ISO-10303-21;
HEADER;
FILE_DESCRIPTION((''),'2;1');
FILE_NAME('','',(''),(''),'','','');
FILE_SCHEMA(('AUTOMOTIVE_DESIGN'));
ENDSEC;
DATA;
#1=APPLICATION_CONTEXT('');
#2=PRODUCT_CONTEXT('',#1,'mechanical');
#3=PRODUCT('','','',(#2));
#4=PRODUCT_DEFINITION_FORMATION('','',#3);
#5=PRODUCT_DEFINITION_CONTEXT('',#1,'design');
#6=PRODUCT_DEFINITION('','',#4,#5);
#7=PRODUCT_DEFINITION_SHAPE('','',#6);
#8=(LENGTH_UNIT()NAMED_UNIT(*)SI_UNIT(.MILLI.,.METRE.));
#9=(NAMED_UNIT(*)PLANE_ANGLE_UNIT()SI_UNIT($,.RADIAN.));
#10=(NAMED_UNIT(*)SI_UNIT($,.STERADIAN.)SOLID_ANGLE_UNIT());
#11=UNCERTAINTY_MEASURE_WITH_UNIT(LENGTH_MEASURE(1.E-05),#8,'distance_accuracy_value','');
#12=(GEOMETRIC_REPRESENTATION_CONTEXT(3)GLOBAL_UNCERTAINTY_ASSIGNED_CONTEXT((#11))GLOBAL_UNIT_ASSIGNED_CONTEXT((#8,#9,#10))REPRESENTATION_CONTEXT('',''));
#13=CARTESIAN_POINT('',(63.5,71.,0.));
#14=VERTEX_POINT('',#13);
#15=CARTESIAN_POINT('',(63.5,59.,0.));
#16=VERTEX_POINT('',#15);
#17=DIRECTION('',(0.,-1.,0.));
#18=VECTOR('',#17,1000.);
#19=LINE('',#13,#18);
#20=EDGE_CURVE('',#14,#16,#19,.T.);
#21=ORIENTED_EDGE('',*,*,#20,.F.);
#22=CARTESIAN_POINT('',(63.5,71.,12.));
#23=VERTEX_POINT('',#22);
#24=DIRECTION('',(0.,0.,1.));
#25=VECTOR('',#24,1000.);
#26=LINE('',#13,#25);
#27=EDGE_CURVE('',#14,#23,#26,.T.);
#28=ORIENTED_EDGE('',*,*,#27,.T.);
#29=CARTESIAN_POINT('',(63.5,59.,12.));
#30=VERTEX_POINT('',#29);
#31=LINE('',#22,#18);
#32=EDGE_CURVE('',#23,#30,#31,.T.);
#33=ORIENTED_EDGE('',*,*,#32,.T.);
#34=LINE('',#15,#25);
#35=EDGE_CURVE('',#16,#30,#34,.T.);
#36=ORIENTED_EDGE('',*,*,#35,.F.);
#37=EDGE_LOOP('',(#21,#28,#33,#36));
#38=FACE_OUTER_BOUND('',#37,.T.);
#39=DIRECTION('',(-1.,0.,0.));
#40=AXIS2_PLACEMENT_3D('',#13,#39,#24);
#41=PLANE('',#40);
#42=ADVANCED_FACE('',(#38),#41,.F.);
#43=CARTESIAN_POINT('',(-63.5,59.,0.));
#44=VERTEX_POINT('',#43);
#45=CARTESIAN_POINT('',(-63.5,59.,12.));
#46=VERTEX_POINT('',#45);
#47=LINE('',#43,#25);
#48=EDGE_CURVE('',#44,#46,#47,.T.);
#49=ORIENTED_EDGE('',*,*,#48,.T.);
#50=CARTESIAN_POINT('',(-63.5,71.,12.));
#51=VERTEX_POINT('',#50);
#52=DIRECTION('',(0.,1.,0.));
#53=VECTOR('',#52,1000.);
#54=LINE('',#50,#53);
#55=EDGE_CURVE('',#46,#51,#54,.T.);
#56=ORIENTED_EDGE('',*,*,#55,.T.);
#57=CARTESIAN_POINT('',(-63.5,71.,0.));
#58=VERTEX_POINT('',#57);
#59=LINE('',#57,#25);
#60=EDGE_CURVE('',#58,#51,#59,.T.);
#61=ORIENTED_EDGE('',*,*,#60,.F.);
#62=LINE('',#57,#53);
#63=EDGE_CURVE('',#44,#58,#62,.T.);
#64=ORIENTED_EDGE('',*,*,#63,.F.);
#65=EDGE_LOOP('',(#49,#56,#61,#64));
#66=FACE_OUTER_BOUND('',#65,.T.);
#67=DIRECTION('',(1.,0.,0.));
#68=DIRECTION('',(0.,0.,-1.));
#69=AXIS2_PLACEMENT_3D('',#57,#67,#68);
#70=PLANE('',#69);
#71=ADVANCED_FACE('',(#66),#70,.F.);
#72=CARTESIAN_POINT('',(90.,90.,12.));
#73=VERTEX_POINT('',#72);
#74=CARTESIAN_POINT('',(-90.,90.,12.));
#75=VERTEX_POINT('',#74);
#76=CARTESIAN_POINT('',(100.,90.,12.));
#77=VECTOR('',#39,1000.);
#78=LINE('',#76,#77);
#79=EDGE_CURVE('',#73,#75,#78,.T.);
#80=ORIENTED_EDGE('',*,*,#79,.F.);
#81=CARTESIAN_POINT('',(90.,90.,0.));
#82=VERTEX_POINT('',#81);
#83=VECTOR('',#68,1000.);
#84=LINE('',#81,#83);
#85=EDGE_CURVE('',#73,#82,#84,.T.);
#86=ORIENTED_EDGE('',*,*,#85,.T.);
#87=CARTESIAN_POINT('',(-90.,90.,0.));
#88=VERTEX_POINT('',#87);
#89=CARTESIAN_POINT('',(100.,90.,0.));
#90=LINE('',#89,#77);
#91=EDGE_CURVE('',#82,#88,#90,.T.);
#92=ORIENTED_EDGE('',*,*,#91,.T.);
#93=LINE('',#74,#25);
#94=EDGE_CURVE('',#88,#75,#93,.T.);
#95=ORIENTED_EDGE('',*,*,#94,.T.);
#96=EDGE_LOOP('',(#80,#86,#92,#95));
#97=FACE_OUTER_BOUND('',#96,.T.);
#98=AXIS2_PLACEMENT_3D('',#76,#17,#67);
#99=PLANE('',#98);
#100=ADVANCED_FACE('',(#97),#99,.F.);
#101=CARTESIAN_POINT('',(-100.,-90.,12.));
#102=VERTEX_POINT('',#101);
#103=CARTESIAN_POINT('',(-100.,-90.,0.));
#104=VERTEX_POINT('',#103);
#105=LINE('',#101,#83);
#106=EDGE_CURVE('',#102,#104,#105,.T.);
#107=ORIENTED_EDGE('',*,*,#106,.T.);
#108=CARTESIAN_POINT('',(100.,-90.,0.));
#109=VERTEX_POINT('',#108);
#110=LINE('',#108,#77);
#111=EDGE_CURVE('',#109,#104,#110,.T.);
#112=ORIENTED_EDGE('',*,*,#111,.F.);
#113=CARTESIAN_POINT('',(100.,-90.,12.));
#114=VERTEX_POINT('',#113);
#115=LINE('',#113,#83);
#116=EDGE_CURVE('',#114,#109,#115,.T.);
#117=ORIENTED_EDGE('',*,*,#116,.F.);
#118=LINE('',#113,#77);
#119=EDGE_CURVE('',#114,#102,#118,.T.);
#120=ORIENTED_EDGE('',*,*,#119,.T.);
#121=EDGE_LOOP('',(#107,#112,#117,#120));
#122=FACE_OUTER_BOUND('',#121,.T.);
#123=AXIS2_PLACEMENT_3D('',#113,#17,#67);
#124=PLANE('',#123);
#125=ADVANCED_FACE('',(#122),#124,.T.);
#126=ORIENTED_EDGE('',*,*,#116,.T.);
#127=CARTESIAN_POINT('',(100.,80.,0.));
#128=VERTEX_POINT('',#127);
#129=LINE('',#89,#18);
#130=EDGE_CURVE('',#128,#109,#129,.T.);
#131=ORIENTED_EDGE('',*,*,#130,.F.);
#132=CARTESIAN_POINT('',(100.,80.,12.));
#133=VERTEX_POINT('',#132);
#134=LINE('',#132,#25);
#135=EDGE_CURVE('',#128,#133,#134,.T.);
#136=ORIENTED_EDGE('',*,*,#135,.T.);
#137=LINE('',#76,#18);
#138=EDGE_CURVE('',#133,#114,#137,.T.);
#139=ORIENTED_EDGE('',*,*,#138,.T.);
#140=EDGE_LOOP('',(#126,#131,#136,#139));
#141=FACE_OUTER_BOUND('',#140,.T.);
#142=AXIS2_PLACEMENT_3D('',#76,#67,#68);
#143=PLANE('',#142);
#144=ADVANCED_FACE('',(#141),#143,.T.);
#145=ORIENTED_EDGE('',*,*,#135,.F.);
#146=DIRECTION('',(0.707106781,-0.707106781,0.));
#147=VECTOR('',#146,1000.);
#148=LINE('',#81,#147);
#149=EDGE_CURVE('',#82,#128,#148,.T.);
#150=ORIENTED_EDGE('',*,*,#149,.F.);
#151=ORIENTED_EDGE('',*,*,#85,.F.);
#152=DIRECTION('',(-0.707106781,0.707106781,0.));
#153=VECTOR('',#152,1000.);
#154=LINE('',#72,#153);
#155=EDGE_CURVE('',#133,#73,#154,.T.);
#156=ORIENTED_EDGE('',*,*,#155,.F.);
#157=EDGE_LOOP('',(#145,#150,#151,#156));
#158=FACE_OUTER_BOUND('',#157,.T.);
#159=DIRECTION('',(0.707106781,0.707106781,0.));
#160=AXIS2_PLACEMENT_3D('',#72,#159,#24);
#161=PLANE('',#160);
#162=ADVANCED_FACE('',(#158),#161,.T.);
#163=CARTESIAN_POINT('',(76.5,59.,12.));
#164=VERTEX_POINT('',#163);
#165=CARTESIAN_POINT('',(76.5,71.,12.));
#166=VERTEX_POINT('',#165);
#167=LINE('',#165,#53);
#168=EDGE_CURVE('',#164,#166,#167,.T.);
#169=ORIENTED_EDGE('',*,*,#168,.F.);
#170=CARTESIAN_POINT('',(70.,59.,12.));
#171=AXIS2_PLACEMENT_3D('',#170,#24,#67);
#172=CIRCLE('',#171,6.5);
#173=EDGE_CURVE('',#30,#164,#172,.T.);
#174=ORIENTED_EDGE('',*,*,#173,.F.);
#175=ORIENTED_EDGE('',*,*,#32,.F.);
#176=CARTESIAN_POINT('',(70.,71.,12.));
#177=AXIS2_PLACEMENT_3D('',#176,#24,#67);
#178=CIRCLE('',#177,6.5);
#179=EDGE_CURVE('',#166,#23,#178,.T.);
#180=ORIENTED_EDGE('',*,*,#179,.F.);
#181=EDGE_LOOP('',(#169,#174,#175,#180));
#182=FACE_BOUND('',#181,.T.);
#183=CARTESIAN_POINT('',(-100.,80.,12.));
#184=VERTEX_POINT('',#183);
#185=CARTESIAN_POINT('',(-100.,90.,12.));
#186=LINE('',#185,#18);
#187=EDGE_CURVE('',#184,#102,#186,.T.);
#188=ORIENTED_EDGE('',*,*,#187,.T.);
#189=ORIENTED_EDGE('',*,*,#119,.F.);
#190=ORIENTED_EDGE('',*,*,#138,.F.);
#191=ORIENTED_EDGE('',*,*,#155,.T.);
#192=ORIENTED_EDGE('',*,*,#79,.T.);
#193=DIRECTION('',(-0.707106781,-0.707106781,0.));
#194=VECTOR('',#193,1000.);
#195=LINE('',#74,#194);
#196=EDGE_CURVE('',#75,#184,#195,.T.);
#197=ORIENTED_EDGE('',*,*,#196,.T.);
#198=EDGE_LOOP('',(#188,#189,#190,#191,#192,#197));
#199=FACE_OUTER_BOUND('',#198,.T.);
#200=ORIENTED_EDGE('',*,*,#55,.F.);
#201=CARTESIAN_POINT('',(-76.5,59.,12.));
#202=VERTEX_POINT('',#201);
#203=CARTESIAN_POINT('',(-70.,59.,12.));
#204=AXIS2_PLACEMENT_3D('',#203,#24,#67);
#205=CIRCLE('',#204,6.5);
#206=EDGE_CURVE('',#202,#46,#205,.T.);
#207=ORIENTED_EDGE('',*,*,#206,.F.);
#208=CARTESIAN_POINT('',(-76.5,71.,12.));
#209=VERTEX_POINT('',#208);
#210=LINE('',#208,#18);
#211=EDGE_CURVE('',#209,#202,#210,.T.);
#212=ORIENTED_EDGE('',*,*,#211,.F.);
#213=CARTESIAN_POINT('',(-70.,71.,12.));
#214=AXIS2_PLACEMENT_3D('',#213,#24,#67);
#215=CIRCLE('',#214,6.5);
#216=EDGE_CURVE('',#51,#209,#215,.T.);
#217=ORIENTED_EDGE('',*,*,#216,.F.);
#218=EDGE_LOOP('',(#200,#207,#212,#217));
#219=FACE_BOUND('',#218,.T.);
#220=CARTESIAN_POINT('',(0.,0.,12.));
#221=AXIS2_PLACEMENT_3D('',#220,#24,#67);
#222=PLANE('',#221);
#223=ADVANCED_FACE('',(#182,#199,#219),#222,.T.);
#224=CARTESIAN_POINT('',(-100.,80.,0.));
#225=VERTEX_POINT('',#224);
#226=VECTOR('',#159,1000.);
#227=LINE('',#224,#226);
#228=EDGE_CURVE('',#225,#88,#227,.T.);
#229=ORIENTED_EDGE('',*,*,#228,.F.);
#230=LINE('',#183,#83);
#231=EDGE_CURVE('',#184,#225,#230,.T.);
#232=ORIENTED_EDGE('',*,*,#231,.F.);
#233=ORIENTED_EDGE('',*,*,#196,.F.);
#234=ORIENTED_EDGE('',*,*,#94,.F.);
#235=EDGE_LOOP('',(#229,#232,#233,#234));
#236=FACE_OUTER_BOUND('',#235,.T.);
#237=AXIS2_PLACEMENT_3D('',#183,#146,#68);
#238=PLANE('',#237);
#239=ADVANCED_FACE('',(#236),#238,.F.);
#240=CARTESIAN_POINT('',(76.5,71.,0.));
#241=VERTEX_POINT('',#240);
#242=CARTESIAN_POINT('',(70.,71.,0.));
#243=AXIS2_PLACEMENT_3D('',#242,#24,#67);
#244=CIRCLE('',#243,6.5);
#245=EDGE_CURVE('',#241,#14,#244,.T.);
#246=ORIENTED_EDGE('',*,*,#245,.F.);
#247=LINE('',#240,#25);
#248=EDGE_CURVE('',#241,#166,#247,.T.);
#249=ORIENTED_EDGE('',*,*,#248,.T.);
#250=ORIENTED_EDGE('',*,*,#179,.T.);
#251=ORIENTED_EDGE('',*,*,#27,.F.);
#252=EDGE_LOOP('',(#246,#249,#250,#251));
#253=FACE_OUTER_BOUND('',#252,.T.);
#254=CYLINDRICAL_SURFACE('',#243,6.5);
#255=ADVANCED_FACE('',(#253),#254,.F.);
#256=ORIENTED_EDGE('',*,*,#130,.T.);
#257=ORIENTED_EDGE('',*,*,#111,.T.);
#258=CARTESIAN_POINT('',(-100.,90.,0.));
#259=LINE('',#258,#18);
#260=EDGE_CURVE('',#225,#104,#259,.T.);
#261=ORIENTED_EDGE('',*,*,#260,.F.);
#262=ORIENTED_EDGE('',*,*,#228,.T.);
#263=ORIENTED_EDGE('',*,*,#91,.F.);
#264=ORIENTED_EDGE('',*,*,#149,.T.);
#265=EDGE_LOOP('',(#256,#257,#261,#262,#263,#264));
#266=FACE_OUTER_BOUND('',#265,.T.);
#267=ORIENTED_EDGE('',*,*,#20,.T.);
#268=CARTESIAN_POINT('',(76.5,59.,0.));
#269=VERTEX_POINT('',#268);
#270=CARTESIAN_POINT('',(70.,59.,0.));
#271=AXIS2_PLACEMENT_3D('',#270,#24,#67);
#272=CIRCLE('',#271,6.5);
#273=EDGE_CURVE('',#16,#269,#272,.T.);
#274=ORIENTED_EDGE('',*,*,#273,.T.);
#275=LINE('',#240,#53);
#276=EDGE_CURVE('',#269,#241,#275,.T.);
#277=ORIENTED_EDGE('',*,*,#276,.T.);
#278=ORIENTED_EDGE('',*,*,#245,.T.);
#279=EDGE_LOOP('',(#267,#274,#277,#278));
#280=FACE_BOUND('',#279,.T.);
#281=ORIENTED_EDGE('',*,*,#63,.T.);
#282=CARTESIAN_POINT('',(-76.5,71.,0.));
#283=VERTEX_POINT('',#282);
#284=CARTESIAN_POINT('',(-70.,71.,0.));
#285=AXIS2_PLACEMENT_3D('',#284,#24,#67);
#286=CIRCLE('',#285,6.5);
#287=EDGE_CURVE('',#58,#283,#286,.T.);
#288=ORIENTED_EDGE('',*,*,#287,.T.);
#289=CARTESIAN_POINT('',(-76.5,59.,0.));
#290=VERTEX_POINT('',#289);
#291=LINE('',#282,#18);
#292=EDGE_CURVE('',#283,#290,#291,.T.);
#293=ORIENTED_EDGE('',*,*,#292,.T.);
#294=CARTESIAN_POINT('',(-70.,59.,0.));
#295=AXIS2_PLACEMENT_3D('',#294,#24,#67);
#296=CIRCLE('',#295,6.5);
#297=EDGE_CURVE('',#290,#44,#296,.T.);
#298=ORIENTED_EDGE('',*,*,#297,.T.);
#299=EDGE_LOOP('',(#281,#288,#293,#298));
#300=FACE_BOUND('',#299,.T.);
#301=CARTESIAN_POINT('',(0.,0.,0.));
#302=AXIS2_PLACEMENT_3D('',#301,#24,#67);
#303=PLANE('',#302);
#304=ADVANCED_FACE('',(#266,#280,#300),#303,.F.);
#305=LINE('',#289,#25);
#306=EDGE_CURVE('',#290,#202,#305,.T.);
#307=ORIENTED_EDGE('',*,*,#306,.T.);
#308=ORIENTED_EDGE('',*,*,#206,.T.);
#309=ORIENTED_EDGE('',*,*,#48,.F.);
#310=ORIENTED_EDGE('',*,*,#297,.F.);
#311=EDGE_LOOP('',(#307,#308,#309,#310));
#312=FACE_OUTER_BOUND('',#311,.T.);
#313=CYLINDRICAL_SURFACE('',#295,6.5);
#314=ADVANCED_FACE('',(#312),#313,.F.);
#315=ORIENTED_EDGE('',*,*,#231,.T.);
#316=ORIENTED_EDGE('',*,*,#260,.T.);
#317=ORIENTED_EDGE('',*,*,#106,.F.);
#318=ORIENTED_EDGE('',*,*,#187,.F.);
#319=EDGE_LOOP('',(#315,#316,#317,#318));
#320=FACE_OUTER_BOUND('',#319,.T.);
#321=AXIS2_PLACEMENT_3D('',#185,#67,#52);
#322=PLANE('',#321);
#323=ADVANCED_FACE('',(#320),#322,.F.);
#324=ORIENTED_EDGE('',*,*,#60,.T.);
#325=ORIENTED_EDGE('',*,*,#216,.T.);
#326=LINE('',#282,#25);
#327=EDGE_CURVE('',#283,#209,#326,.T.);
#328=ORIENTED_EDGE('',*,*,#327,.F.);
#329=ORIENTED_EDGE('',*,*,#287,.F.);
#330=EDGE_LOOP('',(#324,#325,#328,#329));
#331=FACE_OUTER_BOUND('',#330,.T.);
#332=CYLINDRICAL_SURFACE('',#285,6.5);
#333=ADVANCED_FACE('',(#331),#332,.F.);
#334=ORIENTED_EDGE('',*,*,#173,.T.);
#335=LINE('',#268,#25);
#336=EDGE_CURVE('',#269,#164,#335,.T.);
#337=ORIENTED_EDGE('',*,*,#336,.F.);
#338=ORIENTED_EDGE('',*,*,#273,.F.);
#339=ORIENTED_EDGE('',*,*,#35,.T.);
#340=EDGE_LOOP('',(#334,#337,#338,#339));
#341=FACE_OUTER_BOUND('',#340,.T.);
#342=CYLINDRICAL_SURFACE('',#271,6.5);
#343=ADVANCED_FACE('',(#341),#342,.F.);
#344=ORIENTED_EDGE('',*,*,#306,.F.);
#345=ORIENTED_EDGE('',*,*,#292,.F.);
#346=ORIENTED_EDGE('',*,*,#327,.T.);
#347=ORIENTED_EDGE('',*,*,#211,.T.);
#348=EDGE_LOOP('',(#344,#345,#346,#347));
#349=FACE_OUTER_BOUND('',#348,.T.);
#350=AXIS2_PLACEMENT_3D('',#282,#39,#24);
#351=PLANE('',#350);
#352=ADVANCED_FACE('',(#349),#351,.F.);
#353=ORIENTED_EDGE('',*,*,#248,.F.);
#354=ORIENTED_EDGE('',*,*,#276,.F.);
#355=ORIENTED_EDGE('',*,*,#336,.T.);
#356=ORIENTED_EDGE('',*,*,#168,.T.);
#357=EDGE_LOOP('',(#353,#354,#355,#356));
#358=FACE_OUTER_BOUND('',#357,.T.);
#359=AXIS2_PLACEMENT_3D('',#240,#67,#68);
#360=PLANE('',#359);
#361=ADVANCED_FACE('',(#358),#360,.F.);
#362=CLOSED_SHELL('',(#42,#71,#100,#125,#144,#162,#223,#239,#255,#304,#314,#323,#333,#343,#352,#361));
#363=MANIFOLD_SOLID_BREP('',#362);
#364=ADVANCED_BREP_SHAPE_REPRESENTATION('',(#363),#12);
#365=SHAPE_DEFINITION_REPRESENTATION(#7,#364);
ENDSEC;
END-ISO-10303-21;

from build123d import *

# Parameters (mm, degrees)
SKETCH1_W           = 200
SKETCH1_H           = 180
BOSS_EXTRUDE1_DEPTH = 12
CHAMFER1_SIZE       = 10
CUT_EXTRUDE1_DEPTH  = 12


with BuildPart() as part:
    # Sketch1 → Boss-Extrude1 (new body)
    with BuildSketch(Plane.XY):
        Rectangle(SKETCH1_W, SKETCH1_H)
    extrude(amount=BOSS_EXTRUDE1_DEPTH)

    # Chamfer1
    chamfer1_edges = [part.edges().sort_by_distance(p)[0] for p in [
        (100, 90, 6),
        (-100, 90, 6),
    ]]
    chamfer(chamfer1_edges, length=CHAMFER1_SIZE)

    # Sketch2 → Cut-Extrude1 (cut)
    with BuildSketch(Plane.XY.offset(12)):
        with BuildLine():
            Line((-63.5, 71), (-63.5, 59))
            ThreePointArc((-63.5, 59), (-70, 52.5), (-76.5, 59))
            Line((-76.5, 59), (-76.5, 71))
            ThreePointArc((-76.5, 71), (-70, 77.5), (-63.5, 71))
        make_face()
        with BuildLine():
            Line((76.5, 71), (76.5, 59))
            ThreePointArc((76.5, 59), (70, 52.5), (63.5, 59))
            Line((63.5, 59), (63.5, 71))
            ThreePointArc((63.5, 71), (70, 77.5), (76.5, 71))
        make_face()
    extrude(amount=-CUT_EXTRUDE1_DEPTH, mode=Mode.SUBTRACT)


solid = part.part
